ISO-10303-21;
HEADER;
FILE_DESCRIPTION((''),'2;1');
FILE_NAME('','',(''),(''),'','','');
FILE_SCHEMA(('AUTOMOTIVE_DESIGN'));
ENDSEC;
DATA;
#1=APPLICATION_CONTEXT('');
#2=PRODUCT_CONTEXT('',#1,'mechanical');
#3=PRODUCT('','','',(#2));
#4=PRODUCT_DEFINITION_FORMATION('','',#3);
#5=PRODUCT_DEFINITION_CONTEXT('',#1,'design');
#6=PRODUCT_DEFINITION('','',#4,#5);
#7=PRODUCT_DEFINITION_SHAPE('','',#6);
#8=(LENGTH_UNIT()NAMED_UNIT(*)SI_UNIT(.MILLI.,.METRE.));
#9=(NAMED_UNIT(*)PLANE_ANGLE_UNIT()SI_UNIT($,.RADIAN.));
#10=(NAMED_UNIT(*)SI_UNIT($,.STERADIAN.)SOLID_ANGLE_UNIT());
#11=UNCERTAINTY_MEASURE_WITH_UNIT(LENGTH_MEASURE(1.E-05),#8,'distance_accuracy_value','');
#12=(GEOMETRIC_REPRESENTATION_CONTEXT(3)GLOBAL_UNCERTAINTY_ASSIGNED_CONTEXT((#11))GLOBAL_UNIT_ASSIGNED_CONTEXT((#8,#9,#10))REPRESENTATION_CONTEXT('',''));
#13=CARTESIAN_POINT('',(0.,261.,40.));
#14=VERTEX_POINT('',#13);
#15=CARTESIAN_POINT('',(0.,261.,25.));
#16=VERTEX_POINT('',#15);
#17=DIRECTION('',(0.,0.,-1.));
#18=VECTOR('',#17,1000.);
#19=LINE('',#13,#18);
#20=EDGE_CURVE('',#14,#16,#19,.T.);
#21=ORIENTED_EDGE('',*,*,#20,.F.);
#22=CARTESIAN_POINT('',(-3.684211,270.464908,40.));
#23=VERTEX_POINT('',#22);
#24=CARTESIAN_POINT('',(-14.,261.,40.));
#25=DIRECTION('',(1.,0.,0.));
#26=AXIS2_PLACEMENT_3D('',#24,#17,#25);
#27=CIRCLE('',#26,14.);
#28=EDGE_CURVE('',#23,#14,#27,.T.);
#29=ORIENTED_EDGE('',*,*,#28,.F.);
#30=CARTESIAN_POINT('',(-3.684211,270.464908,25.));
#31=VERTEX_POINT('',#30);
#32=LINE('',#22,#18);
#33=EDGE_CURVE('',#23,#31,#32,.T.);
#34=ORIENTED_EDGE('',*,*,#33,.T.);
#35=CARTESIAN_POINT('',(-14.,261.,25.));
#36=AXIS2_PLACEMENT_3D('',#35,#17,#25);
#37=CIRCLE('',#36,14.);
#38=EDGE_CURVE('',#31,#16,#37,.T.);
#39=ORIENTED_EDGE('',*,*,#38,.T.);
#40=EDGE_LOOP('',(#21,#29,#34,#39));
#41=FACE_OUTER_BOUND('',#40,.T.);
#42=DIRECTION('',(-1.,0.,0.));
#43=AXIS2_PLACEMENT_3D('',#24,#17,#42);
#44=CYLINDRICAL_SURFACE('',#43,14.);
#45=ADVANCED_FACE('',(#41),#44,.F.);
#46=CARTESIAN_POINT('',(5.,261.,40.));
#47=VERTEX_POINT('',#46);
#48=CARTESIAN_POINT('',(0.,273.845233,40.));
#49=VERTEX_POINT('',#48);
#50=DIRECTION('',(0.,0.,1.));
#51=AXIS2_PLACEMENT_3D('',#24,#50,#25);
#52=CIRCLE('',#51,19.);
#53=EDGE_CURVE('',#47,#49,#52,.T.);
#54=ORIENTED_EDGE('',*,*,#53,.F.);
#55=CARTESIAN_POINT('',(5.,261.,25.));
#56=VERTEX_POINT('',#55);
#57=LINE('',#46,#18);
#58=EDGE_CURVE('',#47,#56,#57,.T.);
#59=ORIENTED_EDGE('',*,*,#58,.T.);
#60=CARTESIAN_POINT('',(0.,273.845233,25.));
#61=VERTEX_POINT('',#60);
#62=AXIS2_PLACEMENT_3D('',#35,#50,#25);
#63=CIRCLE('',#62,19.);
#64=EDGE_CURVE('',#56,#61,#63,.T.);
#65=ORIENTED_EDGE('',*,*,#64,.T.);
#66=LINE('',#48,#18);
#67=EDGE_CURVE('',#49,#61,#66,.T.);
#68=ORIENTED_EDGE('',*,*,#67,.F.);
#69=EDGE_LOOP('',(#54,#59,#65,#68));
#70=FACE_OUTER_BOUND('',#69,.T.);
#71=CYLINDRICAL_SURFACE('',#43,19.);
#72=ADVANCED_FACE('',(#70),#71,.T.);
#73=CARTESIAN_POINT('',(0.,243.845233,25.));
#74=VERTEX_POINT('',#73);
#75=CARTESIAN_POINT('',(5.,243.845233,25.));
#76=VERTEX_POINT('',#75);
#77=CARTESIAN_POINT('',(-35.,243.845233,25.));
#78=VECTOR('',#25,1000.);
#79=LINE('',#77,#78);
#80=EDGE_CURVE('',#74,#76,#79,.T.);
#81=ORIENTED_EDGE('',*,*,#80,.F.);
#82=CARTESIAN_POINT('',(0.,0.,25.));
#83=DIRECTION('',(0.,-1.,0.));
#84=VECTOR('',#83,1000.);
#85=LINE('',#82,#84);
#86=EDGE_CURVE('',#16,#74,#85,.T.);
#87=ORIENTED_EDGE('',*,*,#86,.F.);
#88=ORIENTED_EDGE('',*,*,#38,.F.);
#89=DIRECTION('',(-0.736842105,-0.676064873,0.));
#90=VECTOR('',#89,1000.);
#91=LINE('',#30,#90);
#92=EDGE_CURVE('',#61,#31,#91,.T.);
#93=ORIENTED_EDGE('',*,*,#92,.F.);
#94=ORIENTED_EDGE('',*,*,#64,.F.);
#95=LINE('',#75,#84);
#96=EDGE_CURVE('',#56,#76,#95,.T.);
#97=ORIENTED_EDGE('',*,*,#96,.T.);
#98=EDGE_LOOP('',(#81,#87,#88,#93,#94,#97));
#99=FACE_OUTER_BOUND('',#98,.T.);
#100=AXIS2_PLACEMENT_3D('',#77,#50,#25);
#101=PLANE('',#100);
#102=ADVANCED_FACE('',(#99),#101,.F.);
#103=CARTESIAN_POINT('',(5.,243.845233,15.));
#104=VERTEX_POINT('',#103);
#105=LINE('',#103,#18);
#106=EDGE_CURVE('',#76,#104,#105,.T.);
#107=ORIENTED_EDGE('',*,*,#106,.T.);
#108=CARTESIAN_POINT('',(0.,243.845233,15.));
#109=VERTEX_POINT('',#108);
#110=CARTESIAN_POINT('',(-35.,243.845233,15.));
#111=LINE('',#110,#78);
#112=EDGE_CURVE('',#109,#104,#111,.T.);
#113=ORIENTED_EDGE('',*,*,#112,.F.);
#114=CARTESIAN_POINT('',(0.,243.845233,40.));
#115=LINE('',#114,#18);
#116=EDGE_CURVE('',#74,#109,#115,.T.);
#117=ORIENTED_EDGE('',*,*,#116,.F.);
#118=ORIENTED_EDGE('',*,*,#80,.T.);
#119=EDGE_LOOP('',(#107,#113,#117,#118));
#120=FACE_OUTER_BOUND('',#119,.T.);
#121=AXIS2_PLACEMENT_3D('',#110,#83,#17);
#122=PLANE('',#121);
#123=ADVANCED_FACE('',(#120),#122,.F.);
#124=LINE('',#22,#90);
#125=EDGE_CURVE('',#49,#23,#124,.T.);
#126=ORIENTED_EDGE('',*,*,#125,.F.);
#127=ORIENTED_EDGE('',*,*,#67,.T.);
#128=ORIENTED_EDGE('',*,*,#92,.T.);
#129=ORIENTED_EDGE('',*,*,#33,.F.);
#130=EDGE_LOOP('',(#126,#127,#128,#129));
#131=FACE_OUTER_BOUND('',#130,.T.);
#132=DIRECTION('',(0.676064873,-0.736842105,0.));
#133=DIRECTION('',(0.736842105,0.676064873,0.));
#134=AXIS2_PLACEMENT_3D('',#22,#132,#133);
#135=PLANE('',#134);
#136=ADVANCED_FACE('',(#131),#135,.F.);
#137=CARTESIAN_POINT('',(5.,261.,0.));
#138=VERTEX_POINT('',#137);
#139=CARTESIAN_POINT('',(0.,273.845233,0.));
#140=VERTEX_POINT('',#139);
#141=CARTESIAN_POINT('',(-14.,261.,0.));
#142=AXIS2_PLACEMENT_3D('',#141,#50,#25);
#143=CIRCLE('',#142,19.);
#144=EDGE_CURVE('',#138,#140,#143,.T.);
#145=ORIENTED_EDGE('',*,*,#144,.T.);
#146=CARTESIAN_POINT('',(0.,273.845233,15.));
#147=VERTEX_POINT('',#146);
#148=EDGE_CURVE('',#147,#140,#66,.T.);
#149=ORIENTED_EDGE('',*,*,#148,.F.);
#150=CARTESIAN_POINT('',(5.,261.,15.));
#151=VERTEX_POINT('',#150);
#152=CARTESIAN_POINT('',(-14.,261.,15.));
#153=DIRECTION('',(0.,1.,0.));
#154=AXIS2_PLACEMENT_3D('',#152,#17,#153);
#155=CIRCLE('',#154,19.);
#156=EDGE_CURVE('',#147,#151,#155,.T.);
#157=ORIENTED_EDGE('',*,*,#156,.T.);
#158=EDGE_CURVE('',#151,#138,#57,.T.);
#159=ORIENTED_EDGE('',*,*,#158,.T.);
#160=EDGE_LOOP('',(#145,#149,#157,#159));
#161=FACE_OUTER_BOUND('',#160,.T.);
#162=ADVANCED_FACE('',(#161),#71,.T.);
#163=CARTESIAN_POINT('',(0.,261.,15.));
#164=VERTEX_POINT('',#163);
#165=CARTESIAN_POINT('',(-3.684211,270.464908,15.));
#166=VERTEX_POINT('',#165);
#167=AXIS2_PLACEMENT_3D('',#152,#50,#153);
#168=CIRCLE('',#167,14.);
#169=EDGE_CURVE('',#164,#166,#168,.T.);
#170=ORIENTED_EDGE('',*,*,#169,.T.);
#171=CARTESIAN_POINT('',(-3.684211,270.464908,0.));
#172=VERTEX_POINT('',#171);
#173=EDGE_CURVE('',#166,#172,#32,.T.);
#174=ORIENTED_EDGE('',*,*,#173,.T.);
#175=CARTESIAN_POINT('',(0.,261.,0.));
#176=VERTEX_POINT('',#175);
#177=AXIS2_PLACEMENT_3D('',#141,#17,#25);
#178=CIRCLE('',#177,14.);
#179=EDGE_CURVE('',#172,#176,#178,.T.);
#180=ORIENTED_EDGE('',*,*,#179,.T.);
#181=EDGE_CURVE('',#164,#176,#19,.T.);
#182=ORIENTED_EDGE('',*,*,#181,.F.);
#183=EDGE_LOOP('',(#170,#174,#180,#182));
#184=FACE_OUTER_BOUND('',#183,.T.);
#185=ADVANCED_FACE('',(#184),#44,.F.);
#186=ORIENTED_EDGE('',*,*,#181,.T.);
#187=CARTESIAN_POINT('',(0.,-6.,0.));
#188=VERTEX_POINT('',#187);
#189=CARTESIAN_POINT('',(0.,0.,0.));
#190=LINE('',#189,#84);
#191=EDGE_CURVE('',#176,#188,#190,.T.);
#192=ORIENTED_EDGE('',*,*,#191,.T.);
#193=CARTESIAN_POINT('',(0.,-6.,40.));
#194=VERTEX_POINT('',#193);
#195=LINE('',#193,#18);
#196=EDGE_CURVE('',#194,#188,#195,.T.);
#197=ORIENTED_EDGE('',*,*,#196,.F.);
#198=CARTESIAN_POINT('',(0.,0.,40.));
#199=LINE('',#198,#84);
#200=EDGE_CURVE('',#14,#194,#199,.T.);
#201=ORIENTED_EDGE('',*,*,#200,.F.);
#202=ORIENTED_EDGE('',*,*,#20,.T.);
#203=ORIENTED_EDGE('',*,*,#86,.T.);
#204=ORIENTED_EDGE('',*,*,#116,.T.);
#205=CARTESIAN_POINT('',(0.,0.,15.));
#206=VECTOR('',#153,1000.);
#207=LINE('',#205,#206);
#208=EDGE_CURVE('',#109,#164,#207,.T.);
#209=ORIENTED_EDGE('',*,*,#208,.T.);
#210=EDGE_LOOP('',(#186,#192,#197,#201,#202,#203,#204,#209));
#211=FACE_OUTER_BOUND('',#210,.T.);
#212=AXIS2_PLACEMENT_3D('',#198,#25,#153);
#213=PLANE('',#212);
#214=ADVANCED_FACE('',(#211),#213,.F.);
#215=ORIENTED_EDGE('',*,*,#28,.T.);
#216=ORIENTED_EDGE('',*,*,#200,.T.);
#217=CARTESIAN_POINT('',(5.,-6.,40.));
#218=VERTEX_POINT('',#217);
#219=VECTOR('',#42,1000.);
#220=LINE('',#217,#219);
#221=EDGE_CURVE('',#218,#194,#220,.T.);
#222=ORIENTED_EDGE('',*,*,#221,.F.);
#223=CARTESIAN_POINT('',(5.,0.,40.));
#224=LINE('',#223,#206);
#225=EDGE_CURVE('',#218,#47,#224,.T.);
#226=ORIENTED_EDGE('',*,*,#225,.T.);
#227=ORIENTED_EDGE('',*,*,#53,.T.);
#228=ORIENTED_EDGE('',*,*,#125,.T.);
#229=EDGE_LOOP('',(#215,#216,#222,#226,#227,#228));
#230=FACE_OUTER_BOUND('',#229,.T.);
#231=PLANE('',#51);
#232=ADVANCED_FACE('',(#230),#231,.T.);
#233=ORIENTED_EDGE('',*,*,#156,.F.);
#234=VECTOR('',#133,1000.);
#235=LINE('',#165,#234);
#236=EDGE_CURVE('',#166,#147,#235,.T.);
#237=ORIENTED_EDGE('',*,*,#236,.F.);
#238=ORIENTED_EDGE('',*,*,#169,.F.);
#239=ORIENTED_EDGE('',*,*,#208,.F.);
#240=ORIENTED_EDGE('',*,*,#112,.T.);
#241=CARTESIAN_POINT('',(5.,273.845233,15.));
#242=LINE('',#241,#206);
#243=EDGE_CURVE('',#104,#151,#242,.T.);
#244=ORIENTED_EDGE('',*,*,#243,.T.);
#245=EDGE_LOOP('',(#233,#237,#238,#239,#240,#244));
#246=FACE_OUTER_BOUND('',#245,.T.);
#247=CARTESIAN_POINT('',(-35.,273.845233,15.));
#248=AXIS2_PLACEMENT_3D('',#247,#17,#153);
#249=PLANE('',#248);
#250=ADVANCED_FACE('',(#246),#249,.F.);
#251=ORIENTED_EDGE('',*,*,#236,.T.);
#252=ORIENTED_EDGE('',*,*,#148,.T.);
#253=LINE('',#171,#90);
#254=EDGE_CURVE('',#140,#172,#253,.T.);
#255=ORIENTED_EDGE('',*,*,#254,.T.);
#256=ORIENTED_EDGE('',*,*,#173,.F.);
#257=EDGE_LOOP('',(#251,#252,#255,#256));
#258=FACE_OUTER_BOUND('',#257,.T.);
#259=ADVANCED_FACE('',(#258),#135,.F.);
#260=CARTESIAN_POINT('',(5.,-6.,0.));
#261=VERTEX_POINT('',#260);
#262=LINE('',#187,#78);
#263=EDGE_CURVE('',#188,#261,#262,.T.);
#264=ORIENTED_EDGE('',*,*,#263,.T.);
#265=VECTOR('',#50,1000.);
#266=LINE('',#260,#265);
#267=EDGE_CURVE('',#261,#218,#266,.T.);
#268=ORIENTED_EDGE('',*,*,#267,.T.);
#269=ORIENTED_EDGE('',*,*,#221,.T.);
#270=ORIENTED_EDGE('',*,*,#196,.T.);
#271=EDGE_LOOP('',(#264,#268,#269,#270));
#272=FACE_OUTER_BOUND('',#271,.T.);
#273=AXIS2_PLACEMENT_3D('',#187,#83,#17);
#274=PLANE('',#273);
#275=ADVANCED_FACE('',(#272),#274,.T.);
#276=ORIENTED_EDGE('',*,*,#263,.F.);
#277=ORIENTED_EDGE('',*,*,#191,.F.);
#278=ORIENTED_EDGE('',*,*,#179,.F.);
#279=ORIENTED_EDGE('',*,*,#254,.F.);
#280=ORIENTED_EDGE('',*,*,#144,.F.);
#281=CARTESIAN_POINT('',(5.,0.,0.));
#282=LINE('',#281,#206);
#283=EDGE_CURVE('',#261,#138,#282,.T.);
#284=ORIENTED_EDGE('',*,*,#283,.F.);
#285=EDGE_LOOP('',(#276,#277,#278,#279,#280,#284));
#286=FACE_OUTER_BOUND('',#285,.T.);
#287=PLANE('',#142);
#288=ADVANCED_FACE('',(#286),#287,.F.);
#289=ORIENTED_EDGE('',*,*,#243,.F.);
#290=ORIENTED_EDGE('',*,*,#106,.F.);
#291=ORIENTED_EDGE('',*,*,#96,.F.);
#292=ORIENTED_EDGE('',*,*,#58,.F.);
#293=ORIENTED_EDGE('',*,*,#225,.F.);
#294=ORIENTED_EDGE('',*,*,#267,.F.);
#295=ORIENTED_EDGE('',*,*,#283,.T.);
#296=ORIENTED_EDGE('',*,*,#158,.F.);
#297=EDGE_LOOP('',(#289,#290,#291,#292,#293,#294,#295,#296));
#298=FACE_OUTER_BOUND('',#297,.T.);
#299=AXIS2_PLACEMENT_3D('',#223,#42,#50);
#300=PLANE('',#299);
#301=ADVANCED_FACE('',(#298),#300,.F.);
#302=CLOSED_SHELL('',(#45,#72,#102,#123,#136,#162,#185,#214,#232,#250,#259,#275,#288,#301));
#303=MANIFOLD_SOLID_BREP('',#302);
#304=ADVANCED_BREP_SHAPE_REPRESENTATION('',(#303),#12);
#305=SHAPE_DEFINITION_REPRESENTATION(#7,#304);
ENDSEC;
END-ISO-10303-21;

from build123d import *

# Parameters (mm, degrees)
EXTRUDE_1_DEPTH     = 40
CUT_EXTRUDE_1_DEPTH = 40
SKETCH_3_W          = 5
SKETCH_3_H          = 40
EXTRUDE_3_DEPTH     = 6


with BuildPart() as part:
    # 草图1 → 凸台-拉伸1 (new body)
    with BuildSketch(Plane.XY):
        with BuildLine():
            Line((0, 0), (5, 0))
            Line((5, 0), (5, 261))
            ThreePointArc((5, 261), (3.70593121, 267.892024376), (0, 273.845232579))
            Line((0, 273.845232579), (-3.684210526, 270.464908216))
            ThreePointArc((-3.684210526, 270.464908216), (-0.953524372, 266.078333751), (0, 261))
            Line((0, 261), (0, 0))
        make_face()
    extrude(amount=EXTRUDE_1_DEPTH)

    # 草图2 → 切除-拉伸1 (cut)
    with BuildSketch(Plane(origin=(5, 0, 0), x_dir=(0, 0, -1), z_dir=(1, 0, 0))):
        Polygon((-20, 273.845232579), (-25, 273.845232579), (-25, 243.845232579), (-15, 243.845232579), (-15, 273.845232579), align=None)
    extrude(amount=-CUT_EXTRUDE_1_DEPTH, mode=Mode.SUBTRACT)

    # 草图3 → 凸台-拉伸3 (add)
    with BuildSketch(Plane.XZ):
        with Locations((2.5, 20)):
            Rectangle(SKETCH_3_W, SKETCH_3_H)
    extrude(amount=EXTRUDE_3_DEPTH)


solid = part.part
